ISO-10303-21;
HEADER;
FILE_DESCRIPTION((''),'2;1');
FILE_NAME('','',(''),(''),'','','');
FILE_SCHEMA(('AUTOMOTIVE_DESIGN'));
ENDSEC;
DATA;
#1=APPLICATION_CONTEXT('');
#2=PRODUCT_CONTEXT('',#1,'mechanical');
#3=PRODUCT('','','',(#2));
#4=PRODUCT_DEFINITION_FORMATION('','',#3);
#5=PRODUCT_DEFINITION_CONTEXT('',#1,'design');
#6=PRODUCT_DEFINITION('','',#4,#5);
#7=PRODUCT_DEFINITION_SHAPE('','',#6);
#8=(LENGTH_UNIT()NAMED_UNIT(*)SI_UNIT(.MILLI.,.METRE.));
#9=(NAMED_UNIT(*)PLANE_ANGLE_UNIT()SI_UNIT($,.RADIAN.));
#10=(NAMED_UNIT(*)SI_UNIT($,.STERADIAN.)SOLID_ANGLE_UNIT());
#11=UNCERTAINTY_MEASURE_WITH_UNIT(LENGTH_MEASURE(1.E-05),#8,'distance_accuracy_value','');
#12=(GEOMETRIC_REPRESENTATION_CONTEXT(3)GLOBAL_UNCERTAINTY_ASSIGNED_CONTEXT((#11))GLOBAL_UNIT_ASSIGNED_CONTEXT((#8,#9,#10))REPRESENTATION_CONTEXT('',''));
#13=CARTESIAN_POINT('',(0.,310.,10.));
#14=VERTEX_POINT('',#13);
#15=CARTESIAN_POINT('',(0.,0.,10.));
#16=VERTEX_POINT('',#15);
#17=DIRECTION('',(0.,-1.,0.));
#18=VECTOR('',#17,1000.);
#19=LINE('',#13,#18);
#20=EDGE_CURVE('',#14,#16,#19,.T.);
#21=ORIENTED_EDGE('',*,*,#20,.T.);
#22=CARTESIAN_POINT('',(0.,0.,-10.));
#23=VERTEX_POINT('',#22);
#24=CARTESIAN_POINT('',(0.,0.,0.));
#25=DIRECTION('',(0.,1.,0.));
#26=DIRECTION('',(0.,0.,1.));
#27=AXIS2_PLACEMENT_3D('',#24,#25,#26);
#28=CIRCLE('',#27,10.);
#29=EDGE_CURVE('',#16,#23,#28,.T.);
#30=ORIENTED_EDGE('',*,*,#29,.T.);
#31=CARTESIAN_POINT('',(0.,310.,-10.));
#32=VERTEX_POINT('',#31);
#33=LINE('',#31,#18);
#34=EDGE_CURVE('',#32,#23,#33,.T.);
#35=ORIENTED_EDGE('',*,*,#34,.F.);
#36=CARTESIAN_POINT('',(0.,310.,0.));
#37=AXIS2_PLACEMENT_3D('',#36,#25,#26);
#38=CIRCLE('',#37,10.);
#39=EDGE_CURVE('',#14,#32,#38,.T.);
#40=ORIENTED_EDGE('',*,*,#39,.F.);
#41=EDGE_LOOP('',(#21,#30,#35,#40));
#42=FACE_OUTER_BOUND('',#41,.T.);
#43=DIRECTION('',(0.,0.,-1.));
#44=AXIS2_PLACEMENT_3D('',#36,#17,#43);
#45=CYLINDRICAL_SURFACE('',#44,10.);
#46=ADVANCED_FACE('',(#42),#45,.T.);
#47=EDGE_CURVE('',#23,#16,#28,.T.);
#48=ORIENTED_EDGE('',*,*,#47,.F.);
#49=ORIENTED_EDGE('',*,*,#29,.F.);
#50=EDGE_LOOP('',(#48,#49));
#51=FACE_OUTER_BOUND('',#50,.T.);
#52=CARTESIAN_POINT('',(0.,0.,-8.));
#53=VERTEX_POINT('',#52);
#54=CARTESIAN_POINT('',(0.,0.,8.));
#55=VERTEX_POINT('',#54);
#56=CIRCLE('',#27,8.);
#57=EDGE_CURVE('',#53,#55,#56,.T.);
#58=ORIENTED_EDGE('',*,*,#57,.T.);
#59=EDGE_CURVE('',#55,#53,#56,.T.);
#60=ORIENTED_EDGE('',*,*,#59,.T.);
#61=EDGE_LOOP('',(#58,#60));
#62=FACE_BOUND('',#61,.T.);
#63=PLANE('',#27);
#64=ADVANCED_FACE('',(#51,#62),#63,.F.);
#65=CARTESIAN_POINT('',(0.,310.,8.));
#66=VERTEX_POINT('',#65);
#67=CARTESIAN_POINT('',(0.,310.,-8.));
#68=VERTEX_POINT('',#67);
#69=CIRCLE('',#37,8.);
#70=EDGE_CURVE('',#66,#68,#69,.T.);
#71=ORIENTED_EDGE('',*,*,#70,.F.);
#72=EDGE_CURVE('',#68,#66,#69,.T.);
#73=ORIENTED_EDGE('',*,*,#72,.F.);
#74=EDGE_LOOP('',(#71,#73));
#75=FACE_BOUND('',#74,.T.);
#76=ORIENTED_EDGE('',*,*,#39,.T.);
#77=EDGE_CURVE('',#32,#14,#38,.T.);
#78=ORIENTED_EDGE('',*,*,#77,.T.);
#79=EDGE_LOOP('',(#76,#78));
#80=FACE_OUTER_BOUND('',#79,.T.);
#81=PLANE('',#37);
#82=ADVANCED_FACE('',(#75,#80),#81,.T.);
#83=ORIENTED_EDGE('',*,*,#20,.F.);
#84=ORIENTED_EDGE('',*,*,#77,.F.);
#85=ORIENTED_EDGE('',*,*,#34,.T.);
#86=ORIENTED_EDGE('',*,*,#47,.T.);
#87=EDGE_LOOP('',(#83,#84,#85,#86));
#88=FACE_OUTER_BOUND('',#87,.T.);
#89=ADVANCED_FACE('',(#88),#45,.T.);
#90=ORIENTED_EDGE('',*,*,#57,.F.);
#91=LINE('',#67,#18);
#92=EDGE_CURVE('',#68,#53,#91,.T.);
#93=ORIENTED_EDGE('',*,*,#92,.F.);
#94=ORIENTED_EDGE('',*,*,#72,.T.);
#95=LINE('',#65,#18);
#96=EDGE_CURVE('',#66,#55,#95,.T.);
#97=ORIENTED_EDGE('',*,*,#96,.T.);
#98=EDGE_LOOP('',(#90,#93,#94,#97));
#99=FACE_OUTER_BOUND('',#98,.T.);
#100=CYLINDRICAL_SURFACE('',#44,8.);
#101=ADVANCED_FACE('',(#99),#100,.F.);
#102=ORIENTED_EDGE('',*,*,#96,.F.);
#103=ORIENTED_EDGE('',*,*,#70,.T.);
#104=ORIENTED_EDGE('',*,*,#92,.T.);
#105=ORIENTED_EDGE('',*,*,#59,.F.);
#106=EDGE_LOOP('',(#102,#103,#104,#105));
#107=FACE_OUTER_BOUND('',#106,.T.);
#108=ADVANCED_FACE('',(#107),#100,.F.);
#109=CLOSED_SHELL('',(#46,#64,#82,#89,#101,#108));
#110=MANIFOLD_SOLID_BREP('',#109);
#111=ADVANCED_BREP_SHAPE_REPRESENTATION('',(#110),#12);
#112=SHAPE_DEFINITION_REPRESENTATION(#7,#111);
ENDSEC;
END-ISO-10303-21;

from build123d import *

# Parameters (mm, degrees)
SKETCH11_R                             = 10
SKETCH11_R_2                           = 8
GB_T_6728_2002_ROUND_TUBE_20_2_1_DEPTH = 310


with BuildPart() as part:
    # Sketch11 → Gb／t 6728—2002 round tube 20 × 2(1) (new body)
    with BuildSketch(Plane(origin=(0, 0, 0), x_dir=(-1, 0, 0), z_dir=(0, 1, 0))):
        Circle(SKETCH11_R)
        Circle(SKETCH11_R_2, mode=Mode.SUBTRACT)
    extrude(amount=GB_T_6728_2002_ROUND_TUBE_20_2_1_DEPTH)


solid = part.part
